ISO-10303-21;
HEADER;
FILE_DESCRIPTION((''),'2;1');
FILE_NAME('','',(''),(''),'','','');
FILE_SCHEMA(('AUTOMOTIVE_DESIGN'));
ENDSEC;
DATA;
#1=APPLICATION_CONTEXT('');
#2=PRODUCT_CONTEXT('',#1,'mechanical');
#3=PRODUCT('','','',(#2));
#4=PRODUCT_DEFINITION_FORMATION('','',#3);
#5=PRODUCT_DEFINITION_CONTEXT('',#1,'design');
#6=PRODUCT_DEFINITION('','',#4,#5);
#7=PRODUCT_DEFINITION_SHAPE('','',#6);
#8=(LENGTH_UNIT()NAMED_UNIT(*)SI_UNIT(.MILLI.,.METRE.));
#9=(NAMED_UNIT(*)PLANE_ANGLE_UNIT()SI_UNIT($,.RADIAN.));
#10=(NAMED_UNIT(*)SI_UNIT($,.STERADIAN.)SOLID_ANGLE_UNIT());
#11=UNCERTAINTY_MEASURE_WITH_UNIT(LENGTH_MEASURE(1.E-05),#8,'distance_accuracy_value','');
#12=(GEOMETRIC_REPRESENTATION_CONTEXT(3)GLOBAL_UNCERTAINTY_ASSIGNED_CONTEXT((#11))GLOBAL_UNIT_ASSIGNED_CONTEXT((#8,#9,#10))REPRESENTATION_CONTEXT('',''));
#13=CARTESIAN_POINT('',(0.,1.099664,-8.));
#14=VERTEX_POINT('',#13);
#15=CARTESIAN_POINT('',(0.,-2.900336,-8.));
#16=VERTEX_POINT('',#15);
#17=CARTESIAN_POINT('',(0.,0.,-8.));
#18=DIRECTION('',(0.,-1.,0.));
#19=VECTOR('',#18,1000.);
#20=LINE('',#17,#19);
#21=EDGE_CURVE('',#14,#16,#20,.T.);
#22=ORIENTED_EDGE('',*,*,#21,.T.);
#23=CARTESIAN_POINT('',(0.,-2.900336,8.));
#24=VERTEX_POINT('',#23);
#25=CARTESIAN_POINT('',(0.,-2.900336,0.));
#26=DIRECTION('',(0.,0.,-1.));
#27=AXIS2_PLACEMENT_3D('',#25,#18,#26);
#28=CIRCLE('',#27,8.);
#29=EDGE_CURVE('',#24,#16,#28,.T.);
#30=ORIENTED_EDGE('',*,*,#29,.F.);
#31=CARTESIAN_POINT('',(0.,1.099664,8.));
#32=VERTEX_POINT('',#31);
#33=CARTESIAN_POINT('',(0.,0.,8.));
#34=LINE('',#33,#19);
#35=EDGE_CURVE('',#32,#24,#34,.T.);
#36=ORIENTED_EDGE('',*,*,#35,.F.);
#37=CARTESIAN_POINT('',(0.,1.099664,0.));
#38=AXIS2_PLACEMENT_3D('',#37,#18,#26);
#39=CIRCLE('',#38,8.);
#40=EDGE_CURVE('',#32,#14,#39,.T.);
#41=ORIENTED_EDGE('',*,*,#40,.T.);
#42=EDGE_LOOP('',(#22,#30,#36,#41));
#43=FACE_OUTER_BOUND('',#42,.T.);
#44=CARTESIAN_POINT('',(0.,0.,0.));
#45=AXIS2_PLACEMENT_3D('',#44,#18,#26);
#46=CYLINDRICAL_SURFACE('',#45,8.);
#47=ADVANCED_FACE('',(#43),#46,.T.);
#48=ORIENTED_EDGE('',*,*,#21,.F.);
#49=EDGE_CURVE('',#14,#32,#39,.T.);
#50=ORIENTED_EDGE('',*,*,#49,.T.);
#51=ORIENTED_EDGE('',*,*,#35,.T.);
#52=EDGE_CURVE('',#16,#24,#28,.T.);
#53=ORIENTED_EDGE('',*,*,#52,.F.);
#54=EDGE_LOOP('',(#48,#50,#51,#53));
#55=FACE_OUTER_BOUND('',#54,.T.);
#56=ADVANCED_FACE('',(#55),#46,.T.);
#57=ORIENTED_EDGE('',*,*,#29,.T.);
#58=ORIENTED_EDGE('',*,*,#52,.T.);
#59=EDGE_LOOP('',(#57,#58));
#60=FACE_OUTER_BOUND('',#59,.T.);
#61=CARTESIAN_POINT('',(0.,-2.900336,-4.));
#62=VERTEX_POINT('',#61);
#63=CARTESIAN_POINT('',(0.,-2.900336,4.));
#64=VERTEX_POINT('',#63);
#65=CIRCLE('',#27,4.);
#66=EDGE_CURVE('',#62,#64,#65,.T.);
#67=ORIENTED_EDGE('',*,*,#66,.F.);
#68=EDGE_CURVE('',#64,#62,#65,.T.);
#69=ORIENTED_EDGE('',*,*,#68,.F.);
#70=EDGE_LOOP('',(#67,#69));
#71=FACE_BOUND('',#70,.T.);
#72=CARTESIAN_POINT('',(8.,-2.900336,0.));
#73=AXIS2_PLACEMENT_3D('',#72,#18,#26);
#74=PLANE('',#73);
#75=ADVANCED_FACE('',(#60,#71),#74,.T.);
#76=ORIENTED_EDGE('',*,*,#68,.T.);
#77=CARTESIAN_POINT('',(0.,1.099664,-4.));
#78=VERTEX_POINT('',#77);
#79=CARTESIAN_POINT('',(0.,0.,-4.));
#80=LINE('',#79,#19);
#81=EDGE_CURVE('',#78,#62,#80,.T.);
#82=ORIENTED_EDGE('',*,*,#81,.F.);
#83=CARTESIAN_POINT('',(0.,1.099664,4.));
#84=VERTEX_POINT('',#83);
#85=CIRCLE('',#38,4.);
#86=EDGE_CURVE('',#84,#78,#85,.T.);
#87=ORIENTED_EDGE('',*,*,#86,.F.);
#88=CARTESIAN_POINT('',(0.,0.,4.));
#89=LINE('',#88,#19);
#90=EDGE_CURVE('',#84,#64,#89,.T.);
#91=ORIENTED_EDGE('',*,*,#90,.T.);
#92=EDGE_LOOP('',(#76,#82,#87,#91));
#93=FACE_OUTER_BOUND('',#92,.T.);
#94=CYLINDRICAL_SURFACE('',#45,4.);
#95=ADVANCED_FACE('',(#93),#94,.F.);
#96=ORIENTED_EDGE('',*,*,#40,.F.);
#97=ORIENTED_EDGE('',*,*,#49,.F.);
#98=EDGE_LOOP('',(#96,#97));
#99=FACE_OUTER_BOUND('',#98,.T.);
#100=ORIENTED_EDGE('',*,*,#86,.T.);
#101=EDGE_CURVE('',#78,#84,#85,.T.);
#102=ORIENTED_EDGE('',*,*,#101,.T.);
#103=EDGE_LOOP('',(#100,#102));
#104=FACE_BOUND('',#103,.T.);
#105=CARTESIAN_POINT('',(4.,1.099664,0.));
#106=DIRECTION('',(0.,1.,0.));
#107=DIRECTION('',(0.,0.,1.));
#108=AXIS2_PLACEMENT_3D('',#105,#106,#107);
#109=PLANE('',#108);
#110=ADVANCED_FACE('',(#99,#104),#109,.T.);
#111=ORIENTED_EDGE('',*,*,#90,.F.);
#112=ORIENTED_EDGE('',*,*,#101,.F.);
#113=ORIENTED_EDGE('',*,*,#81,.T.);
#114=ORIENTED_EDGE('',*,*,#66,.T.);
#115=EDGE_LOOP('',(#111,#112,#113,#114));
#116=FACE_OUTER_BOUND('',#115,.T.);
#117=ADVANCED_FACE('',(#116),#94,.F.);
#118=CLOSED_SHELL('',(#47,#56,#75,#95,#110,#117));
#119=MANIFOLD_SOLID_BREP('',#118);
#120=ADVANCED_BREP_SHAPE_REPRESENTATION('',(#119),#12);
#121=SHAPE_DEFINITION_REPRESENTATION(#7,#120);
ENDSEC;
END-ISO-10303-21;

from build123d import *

# Parameters (mm, degrees)
SKETCH_1_W = 4
SKETCH_1_H = 4


with BuildPart() as part:
    # 草图1 → 旋转1 (revolve)
    with BuildSketch(Plane.XY, mode=Mode.PRIVATE) as revolve_1_sk:
        with Locations((6, -0.900336073)):
            Rectangle(SKETCH_1_W, SKETCH_1_H)
    revolve(revolve_1_sk.sketch.rotate(Axis((0, 0, 0), (0, 1, 0)), 90), axis=Axis((0, 0, 0), (0, 1, 0)))


solid = part.part
